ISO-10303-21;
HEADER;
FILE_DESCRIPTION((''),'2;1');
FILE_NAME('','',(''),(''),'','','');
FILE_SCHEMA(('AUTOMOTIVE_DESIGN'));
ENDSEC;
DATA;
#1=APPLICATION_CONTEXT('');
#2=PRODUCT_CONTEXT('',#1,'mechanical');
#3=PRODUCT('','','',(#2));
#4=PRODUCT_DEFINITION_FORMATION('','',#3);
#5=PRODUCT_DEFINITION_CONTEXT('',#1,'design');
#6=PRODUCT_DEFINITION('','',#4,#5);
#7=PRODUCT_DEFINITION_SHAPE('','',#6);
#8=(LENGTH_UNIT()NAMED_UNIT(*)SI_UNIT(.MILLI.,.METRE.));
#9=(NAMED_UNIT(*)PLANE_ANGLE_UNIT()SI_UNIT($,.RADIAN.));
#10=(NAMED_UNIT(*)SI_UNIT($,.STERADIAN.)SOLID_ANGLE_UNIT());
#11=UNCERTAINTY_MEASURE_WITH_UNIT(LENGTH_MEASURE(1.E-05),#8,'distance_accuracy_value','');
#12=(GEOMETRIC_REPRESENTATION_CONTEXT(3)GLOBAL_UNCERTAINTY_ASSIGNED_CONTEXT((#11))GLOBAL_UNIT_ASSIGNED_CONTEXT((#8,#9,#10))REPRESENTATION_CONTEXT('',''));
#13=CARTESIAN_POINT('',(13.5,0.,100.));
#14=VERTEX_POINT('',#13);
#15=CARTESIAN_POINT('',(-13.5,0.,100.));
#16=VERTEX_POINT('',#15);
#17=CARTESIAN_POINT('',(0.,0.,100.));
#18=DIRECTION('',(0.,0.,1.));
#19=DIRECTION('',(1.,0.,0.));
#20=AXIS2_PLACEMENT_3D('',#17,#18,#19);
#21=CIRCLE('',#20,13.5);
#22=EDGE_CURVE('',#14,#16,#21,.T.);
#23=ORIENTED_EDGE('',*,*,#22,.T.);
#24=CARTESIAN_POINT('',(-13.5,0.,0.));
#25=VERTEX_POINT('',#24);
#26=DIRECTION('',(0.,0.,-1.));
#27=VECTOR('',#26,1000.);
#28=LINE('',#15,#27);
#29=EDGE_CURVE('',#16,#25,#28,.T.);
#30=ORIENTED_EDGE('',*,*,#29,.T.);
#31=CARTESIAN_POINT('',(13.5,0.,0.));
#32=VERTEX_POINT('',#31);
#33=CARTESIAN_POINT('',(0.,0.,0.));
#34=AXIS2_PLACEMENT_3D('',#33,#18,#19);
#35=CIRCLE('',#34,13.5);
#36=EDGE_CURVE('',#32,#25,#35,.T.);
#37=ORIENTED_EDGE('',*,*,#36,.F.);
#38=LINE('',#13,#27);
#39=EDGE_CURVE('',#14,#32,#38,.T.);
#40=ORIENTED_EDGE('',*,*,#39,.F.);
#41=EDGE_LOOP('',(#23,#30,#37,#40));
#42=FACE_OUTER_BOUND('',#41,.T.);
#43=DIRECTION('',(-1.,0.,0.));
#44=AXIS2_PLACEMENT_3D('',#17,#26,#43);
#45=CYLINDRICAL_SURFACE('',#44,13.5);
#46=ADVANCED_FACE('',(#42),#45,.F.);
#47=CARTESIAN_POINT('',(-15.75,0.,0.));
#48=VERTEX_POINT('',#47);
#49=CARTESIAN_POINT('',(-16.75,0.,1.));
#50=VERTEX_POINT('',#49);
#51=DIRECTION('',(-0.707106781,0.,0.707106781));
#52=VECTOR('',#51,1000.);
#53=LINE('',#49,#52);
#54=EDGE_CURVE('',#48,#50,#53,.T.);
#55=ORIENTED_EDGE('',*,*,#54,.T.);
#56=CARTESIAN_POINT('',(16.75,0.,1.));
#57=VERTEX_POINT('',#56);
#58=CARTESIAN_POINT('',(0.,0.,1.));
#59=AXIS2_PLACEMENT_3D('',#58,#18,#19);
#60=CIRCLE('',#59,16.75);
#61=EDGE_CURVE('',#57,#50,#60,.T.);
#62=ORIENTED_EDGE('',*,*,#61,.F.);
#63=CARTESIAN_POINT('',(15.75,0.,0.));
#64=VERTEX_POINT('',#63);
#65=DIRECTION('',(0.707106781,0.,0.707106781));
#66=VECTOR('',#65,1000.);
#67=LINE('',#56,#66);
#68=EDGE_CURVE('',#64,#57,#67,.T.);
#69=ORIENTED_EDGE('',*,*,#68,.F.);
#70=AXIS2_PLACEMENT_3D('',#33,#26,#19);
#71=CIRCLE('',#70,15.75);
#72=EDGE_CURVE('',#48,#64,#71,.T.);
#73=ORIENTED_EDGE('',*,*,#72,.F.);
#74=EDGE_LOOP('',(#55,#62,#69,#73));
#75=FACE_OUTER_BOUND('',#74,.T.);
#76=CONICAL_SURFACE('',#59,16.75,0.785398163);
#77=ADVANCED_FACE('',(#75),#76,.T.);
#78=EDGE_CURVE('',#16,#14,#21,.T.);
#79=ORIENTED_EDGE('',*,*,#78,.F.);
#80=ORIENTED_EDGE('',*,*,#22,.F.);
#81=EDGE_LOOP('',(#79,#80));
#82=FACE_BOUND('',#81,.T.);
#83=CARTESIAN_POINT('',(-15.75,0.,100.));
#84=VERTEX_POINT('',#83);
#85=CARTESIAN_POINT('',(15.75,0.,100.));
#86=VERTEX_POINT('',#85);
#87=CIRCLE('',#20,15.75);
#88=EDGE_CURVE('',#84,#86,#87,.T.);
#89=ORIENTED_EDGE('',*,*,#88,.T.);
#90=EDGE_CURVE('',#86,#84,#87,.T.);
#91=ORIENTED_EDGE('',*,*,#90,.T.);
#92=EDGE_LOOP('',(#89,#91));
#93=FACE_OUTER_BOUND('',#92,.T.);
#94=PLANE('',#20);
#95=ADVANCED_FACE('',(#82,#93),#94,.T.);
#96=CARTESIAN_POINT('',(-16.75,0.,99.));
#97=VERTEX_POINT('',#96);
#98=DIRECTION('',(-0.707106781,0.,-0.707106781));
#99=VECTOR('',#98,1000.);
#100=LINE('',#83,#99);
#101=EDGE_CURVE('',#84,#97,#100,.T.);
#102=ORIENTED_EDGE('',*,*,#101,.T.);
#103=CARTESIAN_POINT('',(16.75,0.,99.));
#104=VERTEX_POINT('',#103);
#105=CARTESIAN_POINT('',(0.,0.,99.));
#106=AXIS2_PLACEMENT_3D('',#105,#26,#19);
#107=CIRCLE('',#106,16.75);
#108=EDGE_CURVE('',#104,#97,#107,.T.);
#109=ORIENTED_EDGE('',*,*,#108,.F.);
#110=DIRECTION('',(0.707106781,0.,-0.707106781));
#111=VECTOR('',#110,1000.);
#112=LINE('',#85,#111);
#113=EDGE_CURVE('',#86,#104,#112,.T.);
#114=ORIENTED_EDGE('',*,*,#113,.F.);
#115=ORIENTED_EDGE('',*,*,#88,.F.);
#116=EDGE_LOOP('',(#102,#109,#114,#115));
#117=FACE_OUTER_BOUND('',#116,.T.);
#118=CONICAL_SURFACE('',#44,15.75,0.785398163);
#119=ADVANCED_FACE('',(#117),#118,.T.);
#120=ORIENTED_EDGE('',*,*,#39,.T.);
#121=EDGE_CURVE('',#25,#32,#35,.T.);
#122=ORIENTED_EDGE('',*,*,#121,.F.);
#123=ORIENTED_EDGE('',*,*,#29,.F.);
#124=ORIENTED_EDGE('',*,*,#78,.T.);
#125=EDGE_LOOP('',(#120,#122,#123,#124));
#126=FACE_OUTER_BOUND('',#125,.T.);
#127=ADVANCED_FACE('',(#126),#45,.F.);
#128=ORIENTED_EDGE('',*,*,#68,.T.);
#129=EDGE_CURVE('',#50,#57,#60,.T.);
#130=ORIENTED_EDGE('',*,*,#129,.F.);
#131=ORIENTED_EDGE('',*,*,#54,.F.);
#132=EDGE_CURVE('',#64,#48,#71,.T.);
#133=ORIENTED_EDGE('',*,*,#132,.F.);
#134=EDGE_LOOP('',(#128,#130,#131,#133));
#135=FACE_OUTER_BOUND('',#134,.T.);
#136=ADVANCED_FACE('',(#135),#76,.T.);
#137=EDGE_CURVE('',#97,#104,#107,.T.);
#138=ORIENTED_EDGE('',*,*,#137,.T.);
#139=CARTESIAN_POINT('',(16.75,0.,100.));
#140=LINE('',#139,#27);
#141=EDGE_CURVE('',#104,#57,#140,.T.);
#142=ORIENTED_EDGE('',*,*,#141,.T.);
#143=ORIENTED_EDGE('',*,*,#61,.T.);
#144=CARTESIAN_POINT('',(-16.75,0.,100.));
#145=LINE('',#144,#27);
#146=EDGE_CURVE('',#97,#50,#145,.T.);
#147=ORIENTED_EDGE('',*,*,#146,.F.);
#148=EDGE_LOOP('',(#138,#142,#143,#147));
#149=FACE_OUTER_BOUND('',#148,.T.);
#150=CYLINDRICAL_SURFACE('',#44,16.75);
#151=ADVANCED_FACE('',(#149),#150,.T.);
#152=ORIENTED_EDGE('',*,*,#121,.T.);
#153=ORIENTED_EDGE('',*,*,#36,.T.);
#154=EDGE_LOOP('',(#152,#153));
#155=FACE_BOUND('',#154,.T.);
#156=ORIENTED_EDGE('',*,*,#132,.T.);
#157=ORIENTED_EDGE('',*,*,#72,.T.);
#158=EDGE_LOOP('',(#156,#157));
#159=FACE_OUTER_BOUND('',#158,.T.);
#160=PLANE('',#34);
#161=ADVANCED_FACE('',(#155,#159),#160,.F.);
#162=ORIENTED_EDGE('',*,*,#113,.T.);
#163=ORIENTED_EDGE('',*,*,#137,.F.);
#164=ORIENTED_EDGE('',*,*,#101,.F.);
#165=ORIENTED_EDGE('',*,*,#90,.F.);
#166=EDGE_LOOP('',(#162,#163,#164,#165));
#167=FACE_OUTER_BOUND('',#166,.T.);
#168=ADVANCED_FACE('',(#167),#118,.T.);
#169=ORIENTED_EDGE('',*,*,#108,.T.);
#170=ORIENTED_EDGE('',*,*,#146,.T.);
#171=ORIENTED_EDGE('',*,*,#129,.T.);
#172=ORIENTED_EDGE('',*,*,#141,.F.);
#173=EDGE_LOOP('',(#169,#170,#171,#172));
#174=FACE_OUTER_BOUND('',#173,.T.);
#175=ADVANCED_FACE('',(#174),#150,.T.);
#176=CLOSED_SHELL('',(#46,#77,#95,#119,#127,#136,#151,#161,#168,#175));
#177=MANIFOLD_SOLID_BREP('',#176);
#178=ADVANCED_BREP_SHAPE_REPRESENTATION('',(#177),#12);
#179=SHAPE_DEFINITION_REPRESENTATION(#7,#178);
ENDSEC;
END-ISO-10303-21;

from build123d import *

# Parameters (mm, degrees)
SKETCH_1_R      = 16.75
SKETCH_1_R_2    = 13.5
EXTRUDE_1_DEPTH = 100
CHAMFER_1_SIZE  = 1
CHAMFER_2_SIZE  = 1


with BuildPart() as part:
    # 草图1 → 凸台-拉伸1 (new body)
    with BuildSketch(Plane.XY):
        Circle(SKETCH_1_R)
        Circle(SKETCH_1_R_2, mode=Mode.SUBTRACT)
    extrude(amount=EXTRUDE_1_DEPTH)

    # 倒角1
    chamfer_1_edges = [part.edges().sort_by_distance(p)[0] for p in [
        (-16.75, 0, 100),
    ]]
    chamfer(chamfer_1_edges, length=CHAMFER_1_SIZE)

    # 倒角2
    chamfer_2_edges = [part.edges().sort_by_distance(p)[0] for p in [
        (-16.75, 0, 0),
    ]]
    chamfer(chamfer_2_edges, length=CHAMFER_2_SIZE)


solid = part.part
